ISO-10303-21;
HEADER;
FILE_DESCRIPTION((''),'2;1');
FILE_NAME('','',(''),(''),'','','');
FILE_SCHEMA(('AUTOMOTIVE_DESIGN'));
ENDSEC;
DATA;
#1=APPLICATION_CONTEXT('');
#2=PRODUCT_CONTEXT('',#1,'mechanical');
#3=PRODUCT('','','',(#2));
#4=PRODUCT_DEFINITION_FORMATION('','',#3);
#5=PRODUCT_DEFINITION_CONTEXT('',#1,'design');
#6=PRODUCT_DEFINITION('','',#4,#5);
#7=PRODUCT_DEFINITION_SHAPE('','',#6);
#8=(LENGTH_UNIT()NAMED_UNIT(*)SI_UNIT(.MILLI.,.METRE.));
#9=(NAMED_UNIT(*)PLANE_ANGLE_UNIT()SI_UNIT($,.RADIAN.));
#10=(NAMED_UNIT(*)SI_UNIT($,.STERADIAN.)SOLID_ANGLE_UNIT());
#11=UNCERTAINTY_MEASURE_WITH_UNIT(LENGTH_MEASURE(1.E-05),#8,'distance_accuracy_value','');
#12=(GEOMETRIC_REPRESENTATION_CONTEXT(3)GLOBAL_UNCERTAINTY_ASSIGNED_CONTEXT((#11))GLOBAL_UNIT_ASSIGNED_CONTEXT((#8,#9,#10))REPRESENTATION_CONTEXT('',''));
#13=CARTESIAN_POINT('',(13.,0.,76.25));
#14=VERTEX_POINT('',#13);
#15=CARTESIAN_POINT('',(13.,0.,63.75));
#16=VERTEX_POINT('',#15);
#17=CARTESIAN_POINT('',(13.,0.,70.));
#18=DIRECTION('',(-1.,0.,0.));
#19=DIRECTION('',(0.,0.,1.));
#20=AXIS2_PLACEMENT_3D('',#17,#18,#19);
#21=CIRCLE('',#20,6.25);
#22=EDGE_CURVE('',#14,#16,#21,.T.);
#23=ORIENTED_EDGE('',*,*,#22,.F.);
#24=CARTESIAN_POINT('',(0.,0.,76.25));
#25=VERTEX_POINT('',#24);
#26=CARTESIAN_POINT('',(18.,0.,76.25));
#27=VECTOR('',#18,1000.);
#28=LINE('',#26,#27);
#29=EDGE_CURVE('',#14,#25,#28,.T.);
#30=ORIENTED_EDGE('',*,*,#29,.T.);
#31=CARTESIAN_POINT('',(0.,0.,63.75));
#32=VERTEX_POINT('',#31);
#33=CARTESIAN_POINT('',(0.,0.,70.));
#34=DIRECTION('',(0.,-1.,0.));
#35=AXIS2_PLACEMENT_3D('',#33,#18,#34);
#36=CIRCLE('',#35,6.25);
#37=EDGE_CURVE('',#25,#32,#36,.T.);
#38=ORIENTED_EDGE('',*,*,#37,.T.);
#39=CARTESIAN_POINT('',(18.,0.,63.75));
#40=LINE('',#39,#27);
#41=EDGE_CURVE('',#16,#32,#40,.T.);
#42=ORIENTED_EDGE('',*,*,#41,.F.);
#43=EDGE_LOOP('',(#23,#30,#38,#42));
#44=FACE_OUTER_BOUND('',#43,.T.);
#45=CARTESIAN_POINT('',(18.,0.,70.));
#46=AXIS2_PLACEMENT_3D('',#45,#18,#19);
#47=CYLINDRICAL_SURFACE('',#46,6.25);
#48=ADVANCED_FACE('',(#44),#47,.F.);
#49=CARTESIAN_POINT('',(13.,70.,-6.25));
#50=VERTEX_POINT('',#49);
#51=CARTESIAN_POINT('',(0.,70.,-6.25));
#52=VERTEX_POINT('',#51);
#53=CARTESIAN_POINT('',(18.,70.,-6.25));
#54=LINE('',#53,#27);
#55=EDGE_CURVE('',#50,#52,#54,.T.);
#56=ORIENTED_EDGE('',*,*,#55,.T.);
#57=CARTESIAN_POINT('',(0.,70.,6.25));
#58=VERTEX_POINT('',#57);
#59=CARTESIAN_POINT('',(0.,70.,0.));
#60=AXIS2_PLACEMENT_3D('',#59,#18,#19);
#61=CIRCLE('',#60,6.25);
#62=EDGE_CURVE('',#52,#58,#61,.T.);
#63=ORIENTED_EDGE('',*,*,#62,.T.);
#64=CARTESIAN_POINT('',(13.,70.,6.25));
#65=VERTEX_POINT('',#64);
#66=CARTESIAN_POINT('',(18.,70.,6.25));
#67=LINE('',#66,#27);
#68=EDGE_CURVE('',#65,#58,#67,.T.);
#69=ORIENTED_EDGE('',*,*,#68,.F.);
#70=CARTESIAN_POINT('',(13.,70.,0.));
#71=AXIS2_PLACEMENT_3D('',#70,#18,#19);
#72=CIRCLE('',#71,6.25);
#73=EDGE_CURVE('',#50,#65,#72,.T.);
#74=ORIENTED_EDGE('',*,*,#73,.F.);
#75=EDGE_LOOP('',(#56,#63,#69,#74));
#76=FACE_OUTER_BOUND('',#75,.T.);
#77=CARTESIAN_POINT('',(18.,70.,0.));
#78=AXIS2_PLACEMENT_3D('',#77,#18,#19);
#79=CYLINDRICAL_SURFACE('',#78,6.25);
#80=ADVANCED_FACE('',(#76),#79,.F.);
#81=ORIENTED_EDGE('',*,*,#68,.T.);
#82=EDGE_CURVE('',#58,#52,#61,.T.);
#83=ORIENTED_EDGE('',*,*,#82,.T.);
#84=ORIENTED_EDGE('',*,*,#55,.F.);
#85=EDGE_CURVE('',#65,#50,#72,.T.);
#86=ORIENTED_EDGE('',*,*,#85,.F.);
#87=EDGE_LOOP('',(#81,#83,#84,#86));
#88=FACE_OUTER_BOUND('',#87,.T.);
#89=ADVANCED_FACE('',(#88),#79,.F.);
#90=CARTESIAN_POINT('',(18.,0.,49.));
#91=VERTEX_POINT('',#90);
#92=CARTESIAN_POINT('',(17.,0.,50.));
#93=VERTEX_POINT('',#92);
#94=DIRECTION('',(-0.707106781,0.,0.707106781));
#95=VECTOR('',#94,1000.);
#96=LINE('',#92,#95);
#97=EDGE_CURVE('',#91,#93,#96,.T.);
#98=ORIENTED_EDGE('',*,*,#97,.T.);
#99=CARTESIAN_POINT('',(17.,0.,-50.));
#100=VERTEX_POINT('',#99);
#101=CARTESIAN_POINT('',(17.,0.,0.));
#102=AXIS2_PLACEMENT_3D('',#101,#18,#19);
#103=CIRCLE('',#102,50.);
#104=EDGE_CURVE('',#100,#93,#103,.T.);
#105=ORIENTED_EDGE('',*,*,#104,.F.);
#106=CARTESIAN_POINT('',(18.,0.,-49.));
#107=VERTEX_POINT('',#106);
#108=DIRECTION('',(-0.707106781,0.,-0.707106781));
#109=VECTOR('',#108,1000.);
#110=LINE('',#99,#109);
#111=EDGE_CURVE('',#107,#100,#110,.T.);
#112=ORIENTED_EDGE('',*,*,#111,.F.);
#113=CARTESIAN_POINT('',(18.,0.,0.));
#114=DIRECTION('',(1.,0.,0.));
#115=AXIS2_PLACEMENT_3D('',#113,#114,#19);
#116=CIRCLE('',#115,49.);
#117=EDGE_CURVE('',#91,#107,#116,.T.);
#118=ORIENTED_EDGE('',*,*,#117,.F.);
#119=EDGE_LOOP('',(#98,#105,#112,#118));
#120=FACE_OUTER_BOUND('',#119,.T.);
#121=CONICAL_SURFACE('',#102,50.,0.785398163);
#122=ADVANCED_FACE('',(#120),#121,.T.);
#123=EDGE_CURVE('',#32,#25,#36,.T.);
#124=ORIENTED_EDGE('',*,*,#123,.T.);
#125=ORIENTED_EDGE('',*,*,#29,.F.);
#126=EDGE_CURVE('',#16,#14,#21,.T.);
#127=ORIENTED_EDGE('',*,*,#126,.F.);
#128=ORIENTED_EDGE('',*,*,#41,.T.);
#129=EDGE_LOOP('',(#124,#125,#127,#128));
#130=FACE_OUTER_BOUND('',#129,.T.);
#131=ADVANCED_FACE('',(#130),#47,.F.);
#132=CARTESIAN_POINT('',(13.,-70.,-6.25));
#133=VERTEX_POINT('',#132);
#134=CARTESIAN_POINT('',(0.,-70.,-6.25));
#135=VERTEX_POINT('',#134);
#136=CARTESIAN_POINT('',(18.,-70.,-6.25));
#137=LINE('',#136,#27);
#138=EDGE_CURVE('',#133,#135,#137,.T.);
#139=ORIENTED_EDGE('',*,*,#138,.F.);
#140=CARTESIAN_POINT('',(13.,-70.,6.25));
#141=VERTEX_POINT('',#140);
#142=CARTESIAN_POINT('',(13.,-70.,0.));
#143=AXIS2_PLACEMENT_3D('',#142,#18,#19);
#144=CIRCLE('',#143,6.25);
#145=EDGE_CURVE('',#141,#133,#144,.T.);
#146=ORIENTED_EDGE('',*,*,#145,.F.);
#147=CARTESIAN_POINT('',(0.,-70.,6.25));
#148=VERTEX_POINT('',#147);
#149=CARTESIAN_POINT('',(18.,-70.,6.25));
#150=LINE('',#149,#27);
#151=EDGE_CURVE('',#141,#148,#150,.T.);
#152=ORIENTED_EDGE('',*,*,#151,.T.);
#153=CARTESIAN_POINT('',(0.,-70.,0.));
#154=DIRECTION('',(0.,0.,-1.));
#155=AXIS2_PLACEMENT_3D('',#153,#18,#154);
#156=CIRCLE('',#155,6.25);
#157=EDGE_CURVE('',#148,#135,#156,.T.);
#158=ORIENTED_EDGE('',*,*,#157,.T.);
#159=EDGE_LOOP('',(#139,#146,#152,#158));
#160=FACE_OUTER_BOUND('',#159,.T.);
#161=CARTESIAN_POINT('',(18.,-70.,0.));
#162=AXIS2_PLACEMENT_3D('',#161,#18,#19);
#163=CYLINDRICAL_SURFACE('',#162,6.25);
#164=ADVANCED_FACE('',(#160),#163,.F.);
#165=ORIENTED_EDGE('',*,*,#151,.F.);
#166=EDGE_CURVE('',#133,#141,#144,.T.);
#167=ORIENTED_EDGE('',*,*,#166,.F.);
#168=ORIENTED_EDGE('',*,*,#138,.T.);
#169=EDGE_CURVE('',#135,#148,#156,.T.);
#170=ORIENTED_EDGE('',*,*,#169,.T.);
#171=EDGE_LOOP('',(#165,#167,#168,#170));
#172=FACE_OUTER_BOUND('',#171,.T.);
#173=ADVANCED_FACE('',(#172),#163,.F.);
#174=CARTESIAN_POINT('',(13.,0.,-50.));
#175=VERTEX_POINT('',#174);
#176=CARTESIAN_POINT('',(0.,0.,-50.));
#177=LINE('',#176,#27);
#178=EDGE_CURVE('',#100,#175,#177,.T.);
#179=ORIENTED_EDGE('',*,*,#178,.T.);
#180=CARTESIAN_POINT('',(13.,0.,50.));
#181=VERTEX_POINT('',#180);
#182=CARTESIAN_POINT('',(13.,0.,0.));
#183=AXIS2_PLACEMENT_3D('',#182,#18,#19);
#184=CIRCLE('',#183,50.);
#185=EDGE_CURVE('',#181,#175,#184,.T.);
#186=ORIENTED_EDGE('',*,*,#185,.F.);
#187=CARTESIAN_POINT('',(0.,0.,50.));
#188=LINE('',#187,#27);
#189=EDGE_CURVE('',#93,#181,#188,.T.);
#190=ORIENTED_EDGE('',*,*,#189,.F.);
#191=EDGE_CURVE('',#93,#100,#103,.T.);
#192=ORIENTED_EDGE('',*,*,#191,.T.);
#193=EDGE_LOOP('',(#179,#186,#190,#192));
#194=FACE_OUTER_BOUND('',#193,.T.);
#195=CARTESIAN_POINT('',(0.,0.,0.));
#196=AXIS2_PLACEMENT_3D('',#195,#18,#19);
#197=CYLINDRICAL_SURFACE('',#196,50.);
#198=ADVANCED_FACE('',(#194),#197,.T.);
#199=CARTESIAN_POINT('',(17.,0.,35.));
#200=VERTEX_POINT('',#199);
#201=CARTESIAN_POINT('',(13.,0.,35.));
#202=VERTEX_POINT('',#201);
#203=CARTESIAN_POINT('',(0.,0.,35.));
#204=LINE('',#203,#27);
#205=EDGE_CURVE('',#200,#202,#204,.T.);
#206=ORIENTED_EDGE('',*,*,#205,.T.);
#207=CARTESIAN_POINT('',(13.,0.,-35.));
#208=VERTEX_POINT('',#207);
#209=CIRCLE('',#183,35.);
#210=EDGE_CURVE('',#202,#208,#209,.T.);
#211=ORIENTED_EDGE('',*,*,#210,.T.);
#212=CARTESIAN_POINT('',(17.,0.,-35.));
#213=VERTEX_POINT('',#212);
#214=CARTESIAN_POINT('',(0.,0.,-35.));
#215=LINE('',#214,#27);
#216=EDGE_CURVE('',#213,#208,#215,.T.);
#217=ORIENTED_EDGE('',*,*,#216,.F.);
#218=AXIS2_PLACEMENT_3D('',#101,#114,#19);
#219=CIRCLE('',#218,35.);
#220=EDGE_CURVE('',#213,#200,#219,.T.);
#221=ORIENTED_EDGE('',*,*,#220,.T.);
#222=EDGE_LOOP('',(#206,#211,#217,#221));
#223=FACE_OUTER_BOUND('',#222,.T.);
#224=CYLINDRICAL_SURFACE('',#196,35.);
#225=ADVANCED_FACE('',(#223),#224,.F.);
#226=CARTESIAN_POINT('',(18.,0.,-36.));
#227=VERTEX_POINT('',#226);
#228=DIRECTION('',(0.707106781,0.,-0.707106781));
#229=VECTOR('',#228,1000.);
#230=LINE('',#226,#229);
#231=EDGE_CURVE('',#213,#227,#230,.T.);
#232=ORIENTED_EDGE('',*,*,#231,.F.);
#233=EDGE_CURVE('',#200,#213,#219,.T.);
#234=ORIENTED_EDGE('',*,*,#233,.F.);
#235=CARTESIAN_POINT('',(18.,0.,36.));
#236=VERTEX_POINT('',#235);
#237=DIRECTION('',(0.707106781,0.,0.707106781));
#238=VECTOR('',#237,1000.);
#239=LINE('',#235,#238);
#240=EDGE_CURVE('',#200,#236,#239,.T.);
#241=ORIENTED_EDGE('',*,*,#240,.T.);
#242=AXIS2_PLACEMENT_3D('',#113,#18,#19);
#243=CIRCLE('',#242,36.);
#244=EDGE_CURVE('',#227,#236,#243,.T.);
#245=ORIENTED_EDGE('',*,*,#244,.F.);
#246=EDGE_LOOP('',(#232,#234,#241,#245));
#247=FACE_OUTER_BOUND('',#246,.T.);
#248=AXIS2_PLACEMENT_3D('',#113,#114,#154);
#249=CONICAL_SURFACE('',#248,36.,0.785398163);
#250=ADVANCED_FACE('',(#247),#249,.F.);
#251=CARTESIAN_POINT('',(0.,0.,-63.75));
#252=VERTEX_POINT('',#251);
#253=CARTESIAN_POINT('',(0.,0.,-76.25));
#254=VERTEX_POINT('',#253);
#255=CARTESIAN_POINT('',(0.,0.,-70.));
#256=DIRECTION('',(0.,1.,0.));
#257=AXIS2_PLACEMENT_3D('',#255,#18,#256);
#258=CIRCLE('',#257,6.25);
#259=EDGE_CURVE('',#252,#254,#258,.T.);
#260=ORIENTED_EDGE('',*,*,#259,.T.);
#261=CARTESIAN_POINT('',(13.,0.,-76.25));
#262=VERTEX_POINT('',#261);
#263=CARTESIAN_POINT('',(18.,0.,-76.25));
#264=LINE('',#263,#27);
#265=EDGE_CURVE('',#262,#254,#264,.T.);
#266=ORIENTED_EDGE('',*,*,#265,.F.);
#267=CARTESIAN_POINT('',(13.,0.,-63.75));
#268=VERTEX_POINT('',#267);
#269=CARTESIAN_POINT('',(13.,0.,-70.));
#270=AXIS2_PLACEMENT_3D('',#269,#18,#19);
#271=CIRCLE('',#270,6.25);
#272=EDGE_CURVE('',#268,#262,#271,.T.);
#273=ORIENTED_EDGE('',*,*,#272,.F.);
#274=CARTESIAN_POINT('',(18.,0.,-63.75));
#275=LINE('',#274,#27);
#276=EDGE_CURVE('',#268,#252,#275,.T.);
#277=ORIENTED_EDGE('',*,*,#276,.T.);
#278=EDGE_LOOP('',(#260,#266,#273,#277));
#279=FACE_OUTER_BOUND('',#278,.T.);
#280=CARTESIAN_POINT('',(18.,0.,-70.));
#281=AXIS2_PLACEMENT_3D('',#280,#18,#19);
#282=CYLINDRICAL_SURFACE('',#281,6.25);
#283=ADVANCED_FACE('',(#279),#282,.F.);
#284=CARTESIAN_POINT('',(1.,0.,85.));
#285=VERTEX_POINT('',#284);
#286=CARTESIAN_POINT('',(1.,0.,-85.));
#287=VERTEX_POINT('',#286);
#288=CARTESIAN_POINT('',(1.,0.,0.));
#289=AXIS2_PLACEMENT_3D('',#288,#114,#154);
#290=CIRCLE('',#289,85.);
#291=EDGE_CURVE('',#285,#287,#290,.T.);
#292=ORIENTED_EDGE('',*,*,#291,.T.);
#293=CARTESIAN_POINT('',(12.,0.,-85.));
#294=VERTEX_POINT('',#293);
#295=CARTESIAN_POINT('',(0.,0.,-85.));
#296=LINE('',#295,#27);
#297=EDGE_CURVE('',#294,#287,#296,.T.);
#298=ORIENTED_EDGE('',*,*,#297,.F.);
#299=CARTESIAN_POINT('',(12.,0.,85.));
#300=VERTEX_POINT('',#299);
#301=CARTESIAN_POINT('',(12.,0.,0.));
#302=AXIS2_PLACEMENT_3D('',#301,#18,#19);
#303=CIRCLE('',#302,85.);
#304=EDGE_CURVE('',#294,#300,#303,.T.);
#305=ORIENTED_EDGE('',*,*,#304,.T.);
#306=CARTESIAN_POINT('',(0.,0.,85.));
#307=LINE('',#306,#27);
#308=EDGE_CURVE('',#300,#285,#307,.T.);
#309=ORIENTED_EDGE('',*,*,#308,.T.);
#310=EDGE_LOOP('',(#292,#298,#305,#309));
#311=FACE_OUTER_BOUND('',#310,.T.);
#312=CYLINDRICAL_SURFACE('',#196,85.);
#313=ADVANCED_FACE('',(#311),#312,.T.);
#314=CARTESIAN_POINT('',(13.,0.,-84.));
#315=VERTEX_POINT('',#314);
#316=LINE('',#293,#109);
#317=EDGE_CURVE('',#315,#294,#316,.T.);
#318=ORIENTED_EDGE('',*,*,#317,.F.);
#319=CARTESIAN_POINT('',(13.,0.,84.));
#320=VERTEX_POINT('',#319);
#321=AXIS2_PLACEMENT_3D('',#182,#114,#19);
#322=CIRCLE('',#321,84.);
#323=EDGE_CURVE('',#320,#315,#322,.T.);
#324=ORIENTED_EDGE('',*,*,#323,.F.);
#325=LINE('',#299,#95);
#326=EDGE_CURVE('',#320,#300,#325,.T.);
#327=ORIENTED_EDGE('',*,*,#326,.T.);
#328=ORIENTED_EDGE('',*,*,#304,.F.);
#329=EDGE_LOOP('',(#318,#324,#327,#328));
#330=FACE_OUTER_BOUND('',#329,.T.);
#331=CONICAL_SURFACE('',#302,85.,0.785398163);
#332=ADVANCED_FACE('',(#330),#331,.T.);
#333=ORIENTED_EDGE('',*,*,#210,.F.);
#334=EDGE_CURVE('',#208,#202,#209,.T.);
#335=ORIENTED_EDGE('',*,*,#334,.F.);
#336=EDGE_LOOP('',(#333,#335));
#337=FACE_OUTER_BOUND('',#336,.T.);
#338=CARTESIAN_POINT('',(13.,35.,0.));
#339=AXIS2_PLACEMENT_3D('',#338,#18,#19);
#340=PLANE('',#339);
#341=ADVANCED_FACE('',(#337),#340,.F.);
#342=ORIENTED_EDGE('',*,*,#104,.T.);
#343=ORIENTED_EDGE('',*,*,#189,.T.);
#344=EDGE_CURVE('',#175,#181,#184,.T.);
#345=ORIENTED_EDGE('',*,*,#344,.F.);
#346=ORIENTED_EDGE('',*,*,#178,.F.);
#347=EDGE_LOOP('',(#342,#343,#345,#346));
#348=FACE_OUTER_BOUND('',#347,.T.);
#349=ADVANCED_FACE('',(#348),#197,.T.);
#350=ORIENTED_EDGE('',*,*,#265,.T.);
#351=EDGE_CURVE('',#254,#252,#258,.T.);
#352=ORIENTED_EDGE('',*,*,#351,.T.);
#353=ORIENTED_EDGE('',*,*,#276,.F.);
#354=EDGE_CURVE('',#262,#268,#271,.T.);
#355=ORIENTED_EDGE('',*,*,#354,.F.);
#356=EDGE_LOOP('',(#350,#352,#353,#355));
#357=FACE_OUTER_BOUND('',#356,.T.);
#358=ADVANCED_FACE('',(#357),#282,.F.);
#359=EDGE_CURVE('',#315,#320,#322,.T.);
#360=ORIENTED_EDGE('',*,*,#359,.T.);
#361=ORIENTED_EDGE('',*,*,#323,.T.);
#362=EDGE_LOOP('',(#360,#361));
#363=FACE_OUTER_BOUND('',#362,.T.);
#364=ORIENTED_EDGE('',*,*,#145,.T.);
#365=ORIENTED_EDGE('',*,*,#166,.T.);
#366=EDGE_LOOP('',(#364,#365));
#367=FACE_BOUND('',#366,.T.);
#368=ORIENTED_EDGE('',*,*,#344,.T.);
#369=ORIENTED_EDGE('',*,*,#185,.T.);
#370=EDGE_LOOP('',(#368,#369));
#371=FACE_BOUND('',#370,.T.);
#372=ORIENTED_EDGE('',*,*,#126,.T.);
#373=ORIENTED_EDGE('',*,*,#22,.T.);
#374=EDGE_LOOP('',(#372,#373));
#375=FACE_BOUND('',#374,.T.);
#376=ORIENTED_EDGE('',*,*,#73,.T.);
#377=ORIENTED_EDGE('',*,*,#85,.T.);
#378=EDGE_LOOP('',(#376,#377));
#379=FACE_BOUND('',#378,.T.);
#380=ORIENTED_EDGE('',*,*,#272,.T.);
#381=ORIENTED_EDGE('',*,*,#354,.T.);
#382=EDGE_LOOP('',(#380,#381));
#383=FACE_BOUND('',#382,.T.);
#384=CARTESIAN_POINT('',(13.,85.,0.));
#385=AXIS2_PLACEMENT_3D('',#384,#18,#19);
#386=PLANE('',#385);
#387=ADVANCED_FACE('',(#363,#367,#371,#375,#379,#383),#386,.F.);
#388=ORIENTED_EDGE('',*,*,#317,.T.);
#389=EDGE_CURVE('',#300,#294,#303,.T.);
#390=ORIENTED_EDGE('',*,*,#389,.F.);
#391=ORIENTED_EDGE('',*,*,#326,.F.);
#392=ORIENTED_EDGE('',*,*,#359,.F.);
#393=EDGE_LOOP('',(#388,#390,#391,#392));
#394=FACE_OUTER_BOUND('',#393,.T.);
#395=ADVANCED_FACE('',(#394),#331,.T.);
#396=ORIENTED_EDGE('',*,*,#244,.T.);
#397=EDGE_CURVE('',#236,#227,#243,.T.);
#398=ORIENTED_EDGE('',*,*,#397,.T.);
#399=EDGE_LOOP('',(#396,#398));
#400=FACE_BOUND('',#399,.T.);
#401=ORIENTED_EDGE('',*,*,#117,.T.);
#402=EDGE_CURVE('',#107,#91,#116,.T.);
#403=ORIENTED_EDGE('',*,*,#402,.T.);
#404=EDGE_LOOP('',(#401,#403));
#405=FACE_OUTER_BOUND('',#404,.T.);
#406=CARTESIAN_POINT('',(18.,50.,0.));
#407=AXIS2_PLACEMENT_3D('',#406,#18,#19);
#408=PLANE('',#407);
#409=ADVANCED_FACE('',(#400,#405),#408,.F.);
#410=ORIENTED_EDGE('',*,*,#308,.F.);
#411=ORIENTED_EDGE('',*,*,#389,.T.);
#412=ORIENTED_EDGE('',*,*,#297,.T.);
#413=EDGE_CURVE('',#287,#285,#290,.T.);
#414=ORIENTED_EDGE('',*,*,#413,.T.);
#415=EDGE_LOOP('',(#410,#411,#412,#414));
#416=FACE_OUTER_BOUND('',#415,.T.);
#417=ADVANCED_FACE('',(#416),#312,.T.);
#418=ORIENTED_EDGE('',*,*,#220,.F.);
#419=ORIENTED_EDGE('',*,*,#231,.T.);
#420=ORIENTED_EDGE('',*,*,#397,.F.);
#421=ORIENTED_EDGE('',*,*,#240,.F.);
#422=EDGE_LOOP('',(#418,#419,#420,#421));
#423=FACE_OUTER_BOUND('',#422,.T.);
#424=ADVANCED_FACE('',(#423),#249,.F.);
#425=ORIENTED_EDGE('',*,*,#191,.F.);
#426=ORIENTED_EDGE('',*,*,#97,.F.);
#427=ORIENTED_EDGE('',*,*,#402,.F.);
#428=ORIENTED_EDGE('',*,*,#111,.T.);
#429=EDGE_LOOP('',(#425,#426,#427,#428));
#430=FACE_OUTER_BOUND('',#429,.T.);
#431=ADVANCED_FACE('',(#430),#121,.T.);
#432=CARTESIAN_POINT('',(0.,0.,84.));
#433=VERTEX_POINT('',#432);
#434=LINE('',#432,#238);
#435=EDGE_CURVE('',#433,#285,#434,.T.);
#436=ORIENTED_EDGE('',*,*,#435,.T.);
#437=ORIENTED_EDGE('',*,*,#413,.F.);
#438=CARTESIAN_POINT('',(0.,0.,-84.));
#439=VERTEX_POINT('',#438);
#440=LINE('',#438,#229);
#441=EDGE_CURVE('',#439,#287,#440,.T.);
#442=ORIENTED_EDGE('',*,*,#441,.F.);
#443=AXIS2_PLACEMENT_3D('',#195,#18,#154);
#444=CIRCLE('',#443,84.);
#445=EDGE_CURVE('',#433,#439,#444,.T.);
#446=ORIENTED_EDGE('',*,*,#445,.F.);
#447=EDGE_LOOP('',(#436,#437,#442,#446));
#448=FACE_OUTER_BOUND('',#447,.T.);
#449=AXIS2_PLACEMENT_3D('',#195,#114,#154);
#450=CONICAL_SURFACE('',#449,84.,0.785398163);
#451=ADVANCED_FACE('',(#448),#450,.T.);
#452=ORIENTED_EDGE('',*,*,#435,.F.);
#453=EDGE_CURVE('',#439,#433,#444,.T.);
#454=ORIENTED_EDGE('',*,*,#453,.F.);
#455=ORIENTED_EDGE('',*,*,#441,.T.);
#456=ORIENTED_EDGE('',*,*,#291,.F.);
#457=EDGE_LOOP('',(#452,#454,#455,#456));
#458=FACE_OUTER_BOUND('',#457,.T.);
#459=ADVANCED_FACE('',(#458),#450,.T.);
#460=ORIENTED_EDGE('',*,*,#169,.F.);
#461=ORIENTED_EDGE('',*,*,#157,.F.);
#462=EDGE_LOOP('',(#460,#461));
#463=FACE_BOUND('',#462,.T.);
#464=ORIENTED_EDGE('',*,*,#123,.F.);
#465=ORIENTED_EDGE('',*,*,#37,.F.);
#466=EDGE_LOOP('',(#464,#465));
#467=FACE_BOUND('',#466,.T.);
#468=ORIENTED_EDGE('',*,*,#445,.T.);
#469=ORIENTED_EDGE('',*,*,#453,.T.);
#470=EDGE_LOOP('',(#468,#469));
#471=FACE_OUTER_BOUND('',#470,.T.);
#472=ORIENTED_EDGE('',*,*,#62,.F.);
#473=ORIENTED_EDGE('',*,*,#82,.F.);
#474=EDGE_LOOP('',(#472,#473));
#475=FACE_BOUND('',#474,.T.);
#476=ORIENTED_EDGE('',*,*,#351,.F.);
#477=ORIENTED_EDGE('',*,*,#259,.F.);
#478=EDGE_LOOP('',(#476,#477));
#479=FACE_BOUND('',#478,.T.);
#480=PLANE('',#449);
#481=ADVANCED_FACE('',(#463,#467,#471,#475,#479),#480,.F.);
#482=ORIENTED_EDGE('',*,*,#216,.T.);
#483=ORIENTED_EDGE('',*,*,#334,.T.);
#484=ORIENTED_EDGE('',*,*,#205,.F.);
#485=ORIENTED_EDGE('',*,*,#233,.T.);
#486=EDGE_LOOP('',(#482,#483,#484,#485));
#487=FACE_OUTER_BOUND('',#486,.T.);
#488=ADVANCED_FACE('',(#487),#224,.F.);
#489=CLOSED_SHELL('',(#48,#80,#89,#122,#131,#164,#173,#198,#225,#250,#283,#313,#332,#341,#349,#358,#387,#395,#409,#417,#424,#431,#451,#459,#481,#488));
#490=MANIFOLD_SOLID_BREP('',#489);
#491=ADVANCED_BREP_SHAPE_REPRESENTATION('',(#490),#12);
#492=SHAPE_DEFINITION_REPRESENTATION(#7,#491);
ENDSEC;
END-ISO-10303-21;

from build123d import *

# Parameters (mm, degrees)
SKETCH_2_R               = 6.25
CUT_EXTRUDE_1_DEPTH      = 122.548344291
PATTERN_CIRCULAR_1_COUNT = 4
CHAMFER_1_SIZE           = 1


with BuildPart() as part:
    # 草图1 → 旋转1 (revolve)
    with BuildSketch(Plane.XY, mode=Mode.PRIVATE) as revolve_1_sk:
        Polygon((0, 0), (0, 85), (13, 85), (13, 50), (18, 50), (18, 35), (13, 35), (13, 0), align=None)
    revolve(revolve_1_sk.sketch.rotate(Axis((0, 0, 0), (1, 0, 0)), 90), axis=Axis((0, 0, 0), (1, 0, 0)))

    # 草图2 → 切除-拉伸1 (cut, through all)
    with BuildSketch(Plane.ZY):
        with Locations((0, 70)):
            Circle(SKETCH_2_R)
    cut_extrude_1 = extrude(amount=-CUT_EXTRUDE_1_DEPTH, mode=Mode.SUBTRACT)

    # 阵列(圆周)1: 切除-拉伸1 ×4 about axis
    pattern_circular_1_axis = Axis((0, 0, 0), (1, 0, 0))
    for i in range(1, PATTERN_CIRCULAR_1_COUNT):
        add(cut_extrude_1.rotate(pattern_circular_1_axis, i * 360 / PATTERN_CIRCULAR_1_COUNT), mode=Mode.SUBTRACT)

    # 倒角1
    chamfer_1_edges = [part.edges().sort_by_distance(p)[0] for p in [
        (18, 0, -35),
        (18, 0, -50),
        (13, 0, -85),
        (0, 0, -85),
    ]]
    chamfer(chamfer_1_edges, length=CHAMFER_1_SIZE)


solid = part.part
